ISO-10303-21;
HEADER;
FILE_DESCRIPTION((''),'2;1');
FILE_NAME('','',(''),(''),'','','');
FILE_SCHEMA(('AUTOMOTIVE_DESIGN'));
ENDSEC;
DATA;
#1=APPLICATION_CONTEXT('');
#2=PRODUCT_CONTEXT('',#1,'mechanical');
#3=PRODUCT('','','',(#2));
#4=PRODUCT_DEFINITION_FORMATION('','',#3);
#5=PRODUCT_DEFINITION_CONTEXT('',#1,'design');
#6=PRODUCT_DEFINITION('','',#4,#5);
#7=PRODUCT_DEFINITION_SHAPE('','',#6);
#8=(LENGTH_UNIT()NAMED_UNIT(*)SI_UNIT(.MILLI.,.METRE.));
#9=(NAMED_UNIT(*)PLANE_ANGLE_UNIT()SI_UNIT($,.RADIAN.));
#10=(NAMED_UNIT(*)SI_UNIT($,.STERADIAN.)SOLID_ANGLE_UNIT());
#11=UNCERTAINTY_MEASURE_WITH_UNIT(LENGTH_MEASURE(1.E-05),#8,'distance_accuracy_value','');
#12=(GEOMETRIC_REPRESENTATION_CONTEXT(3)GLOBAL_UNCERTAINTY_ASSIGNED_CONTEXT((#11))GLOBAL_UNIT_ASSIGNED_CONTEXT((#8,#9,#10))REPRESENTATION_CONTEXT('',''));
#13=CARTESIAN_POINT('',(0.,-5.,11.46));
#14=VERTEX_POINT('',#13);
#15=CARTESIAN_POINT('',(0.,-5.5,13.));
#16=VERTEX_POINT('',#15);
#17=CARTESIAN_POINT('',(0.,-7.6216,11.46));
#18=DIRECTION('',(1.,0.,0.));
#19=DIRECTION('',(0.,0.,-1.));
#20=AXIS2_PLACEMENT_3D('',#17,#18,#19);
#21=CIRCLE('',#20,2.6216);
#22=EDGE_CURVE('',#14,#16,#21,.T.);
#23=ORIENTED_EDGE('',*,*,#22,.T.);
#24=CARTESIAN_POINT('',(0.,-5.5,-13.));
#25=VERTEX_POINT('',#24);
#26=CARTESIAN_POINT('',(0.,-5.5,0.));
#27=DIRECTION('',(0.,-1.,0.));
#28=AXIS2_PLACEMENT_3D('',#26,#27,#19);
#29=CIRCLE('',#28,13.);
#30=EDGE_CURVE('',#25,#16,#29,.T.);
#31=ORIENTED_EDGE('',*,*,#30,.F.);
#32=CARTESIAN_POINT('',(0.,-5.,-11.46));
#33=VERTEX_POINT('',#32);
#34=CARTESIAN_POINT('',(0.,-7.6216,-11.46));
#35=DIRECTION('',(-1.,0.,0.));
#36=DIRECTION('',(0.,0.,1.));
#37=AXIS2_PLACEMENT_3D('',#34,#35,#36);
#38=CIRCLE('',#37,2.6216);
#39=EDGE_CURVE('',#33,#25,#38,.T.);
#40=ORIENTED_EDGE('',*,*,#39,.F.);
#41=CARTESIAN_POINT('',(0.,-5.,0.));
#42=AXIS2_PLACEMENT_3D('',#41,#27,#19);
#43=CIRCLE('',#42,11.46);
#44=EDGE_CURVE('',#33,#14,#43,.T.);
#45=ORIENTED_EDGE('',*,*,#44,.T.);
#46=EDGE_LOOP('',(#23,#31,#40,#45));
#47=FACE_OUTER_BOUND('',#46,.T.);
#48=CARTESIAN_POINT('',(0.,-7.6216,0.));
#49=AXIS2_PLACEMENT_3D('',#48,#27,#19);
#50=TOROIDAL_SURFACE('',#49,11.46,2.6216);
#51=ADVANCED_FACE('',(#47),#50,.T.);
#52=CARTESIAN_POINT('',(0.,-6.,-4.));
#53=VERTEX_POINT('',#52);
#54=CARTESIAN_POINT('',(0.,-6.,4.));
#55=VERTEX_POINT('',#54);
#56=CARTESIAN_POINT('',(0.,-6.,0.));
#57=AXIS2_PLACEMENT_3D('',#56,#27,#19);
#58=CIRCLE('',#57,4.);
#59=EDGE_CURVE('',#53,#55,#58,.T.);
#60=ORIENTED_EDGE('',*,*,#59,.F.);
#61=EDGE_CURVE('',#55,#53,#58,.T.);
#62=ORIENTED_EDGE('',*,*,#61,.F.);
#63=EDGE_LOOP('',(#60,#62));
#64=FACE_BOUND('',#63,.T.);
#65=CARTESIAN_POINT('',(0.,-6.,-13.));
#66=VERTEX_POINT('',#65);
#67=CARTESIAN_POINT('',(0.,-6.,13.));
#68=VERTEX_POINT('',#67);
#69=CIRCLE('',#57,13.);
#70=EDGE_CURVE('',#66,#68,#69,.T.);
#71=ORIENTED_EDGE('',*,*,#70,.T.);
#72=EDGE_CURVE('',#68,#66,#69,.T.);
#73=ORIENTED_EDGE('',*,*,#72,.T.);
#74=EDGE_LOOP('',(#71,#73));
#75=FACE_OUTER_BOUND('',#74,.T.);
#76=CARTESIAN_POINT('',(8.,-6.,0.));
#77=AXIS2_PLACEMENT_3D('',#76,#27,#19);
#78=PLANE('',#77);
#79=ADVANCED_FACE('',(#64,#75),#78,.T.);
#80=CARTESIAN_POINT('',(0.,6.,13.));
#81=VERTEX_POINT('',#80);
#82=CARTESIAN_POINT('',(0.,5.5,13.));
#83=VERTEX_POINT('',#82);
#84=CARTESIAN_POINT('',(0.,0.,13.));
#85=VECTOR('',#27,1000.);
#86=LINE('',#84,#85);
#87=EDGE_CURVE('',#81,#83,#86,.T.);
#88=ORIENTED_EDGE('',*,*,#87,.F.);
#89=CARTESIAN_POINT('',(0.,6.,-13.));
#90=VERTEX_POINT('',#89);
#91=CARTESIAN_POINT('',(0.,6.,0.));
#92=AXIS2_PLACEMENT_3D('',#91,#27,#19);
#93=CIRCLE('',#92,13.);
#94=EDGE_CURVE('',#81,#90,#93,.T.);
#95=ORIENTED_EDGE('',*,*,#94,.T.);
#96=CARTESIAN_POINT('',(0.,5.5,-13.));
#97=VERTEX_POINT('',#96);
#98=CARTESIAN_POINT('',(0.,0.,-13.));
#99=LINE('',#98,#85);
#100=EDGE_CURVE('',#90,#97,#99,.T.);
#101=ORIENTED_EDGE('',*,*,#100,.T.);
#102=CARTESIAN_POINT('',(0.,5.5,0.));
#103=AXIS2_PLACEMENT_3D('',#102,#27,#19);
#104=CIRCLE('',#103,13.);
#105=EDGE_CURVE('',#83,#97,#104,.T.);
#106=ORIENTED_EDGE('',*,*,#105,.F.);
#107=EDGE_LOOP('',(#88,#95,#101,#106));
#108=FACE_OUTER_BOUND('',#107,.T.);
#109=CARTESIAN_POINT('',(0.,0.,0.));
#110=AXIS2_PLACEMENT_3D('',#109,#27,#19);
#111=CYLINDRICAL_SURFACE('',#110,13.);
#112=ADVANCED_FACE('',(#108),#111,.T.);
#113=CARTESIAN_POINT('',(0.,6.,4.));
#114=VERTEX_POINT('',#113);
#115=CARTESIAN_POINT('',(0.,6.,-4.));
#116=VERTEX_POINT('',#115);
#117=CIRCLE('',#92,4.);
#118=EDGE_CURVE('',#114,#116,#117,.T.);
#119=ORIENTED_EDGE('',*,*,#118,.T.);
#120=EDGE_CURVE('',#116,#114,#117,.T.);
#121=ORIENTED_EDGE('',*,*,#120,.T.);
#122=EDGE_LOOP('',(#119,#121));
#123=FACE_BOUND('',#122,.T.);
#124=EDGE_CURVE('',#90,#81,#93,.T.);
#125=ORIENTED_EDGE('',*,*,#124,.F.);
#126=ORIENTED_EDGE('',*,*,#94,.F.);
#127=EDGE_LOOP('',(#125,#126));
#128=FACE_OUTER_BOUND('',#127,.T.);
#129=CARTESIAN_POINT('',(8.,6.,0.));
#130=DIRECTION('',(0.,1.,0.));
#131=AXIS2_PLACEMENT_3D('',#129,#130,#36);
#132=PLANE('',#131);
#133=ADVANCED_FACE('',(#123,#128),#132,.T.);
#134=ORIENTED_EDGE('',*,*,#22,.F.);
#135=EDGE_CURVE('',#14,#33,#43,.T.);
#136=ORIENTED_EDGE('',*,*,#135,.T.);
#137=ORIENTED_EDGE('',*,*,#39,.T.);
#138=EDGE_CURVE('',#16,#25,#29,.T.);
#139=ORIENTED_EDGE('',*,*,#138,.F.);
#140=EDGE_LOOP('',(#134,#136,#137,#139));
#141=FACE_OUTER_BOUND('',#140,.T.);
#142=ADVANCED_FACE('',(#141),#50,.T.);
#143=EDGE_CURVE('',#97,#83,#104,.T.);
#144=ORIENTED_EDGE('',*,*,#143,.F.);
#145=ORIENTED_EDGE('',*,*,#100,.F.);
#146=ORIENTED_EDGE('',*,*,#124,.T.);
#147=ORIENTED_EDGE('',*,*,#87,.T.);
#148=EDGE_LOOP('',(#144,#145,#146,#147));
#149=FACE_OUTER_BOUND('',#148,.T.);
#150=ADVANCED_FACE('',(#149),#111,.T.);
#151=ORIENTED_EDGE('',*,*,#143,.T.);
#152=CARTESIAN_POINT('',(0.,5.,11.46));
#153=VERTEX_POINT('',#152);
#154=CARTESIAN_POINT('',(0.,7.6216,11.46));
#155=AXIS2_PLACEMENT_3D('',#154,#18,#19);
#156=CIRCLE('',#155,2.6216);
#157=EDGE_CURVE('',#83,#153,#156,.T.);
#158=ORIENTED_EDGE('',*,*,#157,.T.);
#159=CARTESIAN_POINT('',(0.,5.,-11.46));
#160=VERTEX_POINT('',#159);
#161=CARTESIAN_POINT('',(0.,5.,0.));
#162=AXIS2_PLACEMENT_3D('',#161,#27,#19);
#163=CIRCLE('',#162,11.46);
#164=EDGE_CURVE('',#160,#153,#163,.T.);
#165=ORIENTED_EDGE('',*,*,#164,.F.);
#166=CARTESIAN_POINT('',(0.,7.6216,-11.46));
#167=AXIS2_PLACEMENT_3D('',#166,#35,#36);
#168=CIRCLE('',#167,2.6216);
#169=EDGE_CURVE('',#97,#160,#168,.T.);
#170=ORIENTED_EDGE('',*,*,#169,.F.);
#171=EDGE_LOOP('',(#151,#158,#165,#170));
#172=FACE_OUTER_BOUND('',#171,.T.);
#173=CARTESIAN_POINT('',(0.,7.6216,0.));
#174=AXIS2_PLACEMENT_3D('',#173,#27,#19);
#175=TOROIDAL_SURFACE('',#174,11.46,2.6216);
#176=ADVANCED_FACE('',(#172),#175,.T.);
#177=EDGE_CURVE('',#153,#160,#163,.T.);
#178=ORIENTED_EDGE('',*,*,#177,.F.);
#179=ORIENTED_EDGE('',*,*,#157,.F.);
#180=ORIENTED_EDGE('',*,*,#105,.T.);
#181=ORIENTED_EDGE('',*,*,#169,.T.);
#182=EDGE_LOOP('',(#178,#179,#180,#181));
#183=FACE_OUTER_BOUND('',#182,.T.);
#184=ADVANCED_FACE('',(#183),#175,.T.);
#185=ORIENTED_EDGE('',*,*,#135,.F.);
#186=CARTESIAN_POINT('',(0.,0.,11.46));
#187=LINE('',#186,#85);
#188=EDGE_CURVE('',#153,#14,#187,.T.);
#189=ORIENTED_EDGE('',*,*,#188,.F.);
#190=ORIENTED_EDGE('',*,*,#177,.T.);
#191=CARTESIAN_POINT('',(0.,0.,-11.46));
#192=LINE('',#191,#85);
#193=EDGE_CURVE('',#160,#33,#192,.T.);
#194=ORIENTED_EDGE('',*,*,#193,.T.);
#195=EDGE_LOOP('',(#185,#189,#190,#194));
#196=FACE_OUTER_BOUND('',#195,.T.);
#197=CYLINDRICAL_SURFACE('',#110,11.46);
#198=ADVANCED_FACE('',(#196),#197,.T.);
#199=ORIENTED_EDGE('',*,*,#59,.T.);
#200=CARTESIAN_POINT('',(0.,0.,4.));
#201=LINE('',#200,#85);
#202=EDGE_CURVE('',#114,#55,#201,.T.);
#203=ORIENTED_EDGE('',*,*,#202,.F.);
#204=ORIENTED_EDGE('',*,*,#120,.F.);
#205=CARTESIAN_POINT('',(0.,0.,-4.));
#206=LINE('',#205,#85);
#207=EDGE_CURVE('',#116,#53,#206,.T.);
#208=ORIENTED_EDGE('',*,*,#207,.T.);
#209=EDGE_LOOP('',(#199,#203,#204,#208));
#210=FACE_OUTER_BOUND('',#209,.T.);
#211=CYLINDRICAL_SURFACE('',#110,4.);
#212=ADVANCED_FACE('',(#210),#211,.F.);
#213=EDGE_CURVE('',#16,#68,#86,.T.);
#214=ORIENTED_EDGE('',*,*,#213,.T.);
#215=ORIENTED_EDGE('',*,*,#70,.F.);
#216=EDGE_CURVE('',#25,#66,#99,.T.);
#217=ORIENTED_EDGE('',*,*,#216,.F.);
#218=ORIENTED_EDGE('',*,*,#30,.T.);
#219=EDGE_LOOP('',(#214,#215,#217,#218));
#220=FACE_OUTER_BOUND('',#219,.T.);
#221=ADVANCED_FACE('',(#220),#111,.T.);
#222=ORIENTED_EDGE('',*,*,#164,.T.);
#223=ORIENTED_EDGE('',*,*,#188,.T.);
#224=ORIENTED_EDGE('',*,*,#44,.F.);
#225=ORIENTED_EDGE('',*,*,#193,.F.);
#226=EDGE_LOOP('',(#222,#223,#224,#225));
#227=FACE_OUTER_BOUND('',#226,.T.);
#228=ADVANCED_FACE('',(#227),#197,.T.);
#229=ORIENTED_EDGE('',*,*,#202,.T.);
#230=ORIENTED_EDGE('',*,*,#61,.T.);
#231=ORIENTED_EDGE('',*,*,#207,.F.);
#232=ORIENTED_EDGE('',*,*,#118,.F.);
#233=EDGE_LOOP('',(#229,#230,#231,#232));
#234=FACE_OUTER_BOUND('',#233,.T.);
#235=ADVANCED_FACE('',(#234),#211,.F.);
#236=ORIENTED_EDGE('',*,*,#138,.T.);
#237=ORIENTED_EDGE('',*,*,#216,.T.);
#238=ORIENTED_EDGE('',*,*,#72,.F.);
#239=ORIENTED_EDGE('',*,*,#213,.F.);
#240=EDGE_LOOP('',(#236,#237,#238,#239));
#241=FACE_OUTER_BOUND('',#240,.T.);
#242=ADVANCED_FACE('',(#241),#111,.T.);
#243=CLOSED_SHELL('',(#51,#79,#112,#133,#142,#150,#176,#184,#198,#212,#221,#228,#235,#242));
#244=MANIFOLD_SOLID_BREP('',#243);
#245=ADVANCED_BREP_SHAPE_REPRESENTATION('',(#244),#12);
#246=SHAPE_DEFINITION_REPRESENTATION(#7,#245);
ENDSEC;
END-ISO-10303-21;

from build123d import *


with BuildPart() as part:
    # Sketch1 → Revolve1 (revolve)
    with BuildSketch(Plane.XY, mode=Mode.PRIVATE) as revolve1_sk:
        Polygon((11.46, -5), (11.46, 5), (8, 5), (8, 6), (4, 6), (4, -6), (8, -6), (8, -5), align=None)
    revolve(revolve1_sk.sketch.rotate(Axis((0, 0, 0), (0, 1, 0)), 90), axis=Axis((0, 0, 0), (0, 1, 0)))

    # Sketch2 → Revolve2 (revolve)
    with BuildSketch(Plane.XY, mode=Mode.PRIVATE) as revolve2_sk:
        with BuildLine():
            Line((8, 5), (11.46, 5))
            ThreePointArc((11.46, 5), (12.269567786, 5.128131219), (13, 5.5))
            Line((13, 5.5), (13, 6))
            Line((13, 6), (8, 6))
            Line((8, 6), (8, 5))
        make_face()
        with BuildLine():
            Line((13, -5.5), (13, -6))
            Line((13, -6), (8, -6))
            Line((8, -6), (8, -5))
            Line((8, -5), (11.46, -5))
            ThreePointArc((11.46, -5), (12.269567786, -5.128131219), (13, -5.5))
        make_face()
    revolve(revolve2_sk.sketch.rotate(Axis((0, 0, 0), (0, 1, 0)), 90), axis=Axis((0, 0, 0), (0, 1, 0)))


solid = part.part
